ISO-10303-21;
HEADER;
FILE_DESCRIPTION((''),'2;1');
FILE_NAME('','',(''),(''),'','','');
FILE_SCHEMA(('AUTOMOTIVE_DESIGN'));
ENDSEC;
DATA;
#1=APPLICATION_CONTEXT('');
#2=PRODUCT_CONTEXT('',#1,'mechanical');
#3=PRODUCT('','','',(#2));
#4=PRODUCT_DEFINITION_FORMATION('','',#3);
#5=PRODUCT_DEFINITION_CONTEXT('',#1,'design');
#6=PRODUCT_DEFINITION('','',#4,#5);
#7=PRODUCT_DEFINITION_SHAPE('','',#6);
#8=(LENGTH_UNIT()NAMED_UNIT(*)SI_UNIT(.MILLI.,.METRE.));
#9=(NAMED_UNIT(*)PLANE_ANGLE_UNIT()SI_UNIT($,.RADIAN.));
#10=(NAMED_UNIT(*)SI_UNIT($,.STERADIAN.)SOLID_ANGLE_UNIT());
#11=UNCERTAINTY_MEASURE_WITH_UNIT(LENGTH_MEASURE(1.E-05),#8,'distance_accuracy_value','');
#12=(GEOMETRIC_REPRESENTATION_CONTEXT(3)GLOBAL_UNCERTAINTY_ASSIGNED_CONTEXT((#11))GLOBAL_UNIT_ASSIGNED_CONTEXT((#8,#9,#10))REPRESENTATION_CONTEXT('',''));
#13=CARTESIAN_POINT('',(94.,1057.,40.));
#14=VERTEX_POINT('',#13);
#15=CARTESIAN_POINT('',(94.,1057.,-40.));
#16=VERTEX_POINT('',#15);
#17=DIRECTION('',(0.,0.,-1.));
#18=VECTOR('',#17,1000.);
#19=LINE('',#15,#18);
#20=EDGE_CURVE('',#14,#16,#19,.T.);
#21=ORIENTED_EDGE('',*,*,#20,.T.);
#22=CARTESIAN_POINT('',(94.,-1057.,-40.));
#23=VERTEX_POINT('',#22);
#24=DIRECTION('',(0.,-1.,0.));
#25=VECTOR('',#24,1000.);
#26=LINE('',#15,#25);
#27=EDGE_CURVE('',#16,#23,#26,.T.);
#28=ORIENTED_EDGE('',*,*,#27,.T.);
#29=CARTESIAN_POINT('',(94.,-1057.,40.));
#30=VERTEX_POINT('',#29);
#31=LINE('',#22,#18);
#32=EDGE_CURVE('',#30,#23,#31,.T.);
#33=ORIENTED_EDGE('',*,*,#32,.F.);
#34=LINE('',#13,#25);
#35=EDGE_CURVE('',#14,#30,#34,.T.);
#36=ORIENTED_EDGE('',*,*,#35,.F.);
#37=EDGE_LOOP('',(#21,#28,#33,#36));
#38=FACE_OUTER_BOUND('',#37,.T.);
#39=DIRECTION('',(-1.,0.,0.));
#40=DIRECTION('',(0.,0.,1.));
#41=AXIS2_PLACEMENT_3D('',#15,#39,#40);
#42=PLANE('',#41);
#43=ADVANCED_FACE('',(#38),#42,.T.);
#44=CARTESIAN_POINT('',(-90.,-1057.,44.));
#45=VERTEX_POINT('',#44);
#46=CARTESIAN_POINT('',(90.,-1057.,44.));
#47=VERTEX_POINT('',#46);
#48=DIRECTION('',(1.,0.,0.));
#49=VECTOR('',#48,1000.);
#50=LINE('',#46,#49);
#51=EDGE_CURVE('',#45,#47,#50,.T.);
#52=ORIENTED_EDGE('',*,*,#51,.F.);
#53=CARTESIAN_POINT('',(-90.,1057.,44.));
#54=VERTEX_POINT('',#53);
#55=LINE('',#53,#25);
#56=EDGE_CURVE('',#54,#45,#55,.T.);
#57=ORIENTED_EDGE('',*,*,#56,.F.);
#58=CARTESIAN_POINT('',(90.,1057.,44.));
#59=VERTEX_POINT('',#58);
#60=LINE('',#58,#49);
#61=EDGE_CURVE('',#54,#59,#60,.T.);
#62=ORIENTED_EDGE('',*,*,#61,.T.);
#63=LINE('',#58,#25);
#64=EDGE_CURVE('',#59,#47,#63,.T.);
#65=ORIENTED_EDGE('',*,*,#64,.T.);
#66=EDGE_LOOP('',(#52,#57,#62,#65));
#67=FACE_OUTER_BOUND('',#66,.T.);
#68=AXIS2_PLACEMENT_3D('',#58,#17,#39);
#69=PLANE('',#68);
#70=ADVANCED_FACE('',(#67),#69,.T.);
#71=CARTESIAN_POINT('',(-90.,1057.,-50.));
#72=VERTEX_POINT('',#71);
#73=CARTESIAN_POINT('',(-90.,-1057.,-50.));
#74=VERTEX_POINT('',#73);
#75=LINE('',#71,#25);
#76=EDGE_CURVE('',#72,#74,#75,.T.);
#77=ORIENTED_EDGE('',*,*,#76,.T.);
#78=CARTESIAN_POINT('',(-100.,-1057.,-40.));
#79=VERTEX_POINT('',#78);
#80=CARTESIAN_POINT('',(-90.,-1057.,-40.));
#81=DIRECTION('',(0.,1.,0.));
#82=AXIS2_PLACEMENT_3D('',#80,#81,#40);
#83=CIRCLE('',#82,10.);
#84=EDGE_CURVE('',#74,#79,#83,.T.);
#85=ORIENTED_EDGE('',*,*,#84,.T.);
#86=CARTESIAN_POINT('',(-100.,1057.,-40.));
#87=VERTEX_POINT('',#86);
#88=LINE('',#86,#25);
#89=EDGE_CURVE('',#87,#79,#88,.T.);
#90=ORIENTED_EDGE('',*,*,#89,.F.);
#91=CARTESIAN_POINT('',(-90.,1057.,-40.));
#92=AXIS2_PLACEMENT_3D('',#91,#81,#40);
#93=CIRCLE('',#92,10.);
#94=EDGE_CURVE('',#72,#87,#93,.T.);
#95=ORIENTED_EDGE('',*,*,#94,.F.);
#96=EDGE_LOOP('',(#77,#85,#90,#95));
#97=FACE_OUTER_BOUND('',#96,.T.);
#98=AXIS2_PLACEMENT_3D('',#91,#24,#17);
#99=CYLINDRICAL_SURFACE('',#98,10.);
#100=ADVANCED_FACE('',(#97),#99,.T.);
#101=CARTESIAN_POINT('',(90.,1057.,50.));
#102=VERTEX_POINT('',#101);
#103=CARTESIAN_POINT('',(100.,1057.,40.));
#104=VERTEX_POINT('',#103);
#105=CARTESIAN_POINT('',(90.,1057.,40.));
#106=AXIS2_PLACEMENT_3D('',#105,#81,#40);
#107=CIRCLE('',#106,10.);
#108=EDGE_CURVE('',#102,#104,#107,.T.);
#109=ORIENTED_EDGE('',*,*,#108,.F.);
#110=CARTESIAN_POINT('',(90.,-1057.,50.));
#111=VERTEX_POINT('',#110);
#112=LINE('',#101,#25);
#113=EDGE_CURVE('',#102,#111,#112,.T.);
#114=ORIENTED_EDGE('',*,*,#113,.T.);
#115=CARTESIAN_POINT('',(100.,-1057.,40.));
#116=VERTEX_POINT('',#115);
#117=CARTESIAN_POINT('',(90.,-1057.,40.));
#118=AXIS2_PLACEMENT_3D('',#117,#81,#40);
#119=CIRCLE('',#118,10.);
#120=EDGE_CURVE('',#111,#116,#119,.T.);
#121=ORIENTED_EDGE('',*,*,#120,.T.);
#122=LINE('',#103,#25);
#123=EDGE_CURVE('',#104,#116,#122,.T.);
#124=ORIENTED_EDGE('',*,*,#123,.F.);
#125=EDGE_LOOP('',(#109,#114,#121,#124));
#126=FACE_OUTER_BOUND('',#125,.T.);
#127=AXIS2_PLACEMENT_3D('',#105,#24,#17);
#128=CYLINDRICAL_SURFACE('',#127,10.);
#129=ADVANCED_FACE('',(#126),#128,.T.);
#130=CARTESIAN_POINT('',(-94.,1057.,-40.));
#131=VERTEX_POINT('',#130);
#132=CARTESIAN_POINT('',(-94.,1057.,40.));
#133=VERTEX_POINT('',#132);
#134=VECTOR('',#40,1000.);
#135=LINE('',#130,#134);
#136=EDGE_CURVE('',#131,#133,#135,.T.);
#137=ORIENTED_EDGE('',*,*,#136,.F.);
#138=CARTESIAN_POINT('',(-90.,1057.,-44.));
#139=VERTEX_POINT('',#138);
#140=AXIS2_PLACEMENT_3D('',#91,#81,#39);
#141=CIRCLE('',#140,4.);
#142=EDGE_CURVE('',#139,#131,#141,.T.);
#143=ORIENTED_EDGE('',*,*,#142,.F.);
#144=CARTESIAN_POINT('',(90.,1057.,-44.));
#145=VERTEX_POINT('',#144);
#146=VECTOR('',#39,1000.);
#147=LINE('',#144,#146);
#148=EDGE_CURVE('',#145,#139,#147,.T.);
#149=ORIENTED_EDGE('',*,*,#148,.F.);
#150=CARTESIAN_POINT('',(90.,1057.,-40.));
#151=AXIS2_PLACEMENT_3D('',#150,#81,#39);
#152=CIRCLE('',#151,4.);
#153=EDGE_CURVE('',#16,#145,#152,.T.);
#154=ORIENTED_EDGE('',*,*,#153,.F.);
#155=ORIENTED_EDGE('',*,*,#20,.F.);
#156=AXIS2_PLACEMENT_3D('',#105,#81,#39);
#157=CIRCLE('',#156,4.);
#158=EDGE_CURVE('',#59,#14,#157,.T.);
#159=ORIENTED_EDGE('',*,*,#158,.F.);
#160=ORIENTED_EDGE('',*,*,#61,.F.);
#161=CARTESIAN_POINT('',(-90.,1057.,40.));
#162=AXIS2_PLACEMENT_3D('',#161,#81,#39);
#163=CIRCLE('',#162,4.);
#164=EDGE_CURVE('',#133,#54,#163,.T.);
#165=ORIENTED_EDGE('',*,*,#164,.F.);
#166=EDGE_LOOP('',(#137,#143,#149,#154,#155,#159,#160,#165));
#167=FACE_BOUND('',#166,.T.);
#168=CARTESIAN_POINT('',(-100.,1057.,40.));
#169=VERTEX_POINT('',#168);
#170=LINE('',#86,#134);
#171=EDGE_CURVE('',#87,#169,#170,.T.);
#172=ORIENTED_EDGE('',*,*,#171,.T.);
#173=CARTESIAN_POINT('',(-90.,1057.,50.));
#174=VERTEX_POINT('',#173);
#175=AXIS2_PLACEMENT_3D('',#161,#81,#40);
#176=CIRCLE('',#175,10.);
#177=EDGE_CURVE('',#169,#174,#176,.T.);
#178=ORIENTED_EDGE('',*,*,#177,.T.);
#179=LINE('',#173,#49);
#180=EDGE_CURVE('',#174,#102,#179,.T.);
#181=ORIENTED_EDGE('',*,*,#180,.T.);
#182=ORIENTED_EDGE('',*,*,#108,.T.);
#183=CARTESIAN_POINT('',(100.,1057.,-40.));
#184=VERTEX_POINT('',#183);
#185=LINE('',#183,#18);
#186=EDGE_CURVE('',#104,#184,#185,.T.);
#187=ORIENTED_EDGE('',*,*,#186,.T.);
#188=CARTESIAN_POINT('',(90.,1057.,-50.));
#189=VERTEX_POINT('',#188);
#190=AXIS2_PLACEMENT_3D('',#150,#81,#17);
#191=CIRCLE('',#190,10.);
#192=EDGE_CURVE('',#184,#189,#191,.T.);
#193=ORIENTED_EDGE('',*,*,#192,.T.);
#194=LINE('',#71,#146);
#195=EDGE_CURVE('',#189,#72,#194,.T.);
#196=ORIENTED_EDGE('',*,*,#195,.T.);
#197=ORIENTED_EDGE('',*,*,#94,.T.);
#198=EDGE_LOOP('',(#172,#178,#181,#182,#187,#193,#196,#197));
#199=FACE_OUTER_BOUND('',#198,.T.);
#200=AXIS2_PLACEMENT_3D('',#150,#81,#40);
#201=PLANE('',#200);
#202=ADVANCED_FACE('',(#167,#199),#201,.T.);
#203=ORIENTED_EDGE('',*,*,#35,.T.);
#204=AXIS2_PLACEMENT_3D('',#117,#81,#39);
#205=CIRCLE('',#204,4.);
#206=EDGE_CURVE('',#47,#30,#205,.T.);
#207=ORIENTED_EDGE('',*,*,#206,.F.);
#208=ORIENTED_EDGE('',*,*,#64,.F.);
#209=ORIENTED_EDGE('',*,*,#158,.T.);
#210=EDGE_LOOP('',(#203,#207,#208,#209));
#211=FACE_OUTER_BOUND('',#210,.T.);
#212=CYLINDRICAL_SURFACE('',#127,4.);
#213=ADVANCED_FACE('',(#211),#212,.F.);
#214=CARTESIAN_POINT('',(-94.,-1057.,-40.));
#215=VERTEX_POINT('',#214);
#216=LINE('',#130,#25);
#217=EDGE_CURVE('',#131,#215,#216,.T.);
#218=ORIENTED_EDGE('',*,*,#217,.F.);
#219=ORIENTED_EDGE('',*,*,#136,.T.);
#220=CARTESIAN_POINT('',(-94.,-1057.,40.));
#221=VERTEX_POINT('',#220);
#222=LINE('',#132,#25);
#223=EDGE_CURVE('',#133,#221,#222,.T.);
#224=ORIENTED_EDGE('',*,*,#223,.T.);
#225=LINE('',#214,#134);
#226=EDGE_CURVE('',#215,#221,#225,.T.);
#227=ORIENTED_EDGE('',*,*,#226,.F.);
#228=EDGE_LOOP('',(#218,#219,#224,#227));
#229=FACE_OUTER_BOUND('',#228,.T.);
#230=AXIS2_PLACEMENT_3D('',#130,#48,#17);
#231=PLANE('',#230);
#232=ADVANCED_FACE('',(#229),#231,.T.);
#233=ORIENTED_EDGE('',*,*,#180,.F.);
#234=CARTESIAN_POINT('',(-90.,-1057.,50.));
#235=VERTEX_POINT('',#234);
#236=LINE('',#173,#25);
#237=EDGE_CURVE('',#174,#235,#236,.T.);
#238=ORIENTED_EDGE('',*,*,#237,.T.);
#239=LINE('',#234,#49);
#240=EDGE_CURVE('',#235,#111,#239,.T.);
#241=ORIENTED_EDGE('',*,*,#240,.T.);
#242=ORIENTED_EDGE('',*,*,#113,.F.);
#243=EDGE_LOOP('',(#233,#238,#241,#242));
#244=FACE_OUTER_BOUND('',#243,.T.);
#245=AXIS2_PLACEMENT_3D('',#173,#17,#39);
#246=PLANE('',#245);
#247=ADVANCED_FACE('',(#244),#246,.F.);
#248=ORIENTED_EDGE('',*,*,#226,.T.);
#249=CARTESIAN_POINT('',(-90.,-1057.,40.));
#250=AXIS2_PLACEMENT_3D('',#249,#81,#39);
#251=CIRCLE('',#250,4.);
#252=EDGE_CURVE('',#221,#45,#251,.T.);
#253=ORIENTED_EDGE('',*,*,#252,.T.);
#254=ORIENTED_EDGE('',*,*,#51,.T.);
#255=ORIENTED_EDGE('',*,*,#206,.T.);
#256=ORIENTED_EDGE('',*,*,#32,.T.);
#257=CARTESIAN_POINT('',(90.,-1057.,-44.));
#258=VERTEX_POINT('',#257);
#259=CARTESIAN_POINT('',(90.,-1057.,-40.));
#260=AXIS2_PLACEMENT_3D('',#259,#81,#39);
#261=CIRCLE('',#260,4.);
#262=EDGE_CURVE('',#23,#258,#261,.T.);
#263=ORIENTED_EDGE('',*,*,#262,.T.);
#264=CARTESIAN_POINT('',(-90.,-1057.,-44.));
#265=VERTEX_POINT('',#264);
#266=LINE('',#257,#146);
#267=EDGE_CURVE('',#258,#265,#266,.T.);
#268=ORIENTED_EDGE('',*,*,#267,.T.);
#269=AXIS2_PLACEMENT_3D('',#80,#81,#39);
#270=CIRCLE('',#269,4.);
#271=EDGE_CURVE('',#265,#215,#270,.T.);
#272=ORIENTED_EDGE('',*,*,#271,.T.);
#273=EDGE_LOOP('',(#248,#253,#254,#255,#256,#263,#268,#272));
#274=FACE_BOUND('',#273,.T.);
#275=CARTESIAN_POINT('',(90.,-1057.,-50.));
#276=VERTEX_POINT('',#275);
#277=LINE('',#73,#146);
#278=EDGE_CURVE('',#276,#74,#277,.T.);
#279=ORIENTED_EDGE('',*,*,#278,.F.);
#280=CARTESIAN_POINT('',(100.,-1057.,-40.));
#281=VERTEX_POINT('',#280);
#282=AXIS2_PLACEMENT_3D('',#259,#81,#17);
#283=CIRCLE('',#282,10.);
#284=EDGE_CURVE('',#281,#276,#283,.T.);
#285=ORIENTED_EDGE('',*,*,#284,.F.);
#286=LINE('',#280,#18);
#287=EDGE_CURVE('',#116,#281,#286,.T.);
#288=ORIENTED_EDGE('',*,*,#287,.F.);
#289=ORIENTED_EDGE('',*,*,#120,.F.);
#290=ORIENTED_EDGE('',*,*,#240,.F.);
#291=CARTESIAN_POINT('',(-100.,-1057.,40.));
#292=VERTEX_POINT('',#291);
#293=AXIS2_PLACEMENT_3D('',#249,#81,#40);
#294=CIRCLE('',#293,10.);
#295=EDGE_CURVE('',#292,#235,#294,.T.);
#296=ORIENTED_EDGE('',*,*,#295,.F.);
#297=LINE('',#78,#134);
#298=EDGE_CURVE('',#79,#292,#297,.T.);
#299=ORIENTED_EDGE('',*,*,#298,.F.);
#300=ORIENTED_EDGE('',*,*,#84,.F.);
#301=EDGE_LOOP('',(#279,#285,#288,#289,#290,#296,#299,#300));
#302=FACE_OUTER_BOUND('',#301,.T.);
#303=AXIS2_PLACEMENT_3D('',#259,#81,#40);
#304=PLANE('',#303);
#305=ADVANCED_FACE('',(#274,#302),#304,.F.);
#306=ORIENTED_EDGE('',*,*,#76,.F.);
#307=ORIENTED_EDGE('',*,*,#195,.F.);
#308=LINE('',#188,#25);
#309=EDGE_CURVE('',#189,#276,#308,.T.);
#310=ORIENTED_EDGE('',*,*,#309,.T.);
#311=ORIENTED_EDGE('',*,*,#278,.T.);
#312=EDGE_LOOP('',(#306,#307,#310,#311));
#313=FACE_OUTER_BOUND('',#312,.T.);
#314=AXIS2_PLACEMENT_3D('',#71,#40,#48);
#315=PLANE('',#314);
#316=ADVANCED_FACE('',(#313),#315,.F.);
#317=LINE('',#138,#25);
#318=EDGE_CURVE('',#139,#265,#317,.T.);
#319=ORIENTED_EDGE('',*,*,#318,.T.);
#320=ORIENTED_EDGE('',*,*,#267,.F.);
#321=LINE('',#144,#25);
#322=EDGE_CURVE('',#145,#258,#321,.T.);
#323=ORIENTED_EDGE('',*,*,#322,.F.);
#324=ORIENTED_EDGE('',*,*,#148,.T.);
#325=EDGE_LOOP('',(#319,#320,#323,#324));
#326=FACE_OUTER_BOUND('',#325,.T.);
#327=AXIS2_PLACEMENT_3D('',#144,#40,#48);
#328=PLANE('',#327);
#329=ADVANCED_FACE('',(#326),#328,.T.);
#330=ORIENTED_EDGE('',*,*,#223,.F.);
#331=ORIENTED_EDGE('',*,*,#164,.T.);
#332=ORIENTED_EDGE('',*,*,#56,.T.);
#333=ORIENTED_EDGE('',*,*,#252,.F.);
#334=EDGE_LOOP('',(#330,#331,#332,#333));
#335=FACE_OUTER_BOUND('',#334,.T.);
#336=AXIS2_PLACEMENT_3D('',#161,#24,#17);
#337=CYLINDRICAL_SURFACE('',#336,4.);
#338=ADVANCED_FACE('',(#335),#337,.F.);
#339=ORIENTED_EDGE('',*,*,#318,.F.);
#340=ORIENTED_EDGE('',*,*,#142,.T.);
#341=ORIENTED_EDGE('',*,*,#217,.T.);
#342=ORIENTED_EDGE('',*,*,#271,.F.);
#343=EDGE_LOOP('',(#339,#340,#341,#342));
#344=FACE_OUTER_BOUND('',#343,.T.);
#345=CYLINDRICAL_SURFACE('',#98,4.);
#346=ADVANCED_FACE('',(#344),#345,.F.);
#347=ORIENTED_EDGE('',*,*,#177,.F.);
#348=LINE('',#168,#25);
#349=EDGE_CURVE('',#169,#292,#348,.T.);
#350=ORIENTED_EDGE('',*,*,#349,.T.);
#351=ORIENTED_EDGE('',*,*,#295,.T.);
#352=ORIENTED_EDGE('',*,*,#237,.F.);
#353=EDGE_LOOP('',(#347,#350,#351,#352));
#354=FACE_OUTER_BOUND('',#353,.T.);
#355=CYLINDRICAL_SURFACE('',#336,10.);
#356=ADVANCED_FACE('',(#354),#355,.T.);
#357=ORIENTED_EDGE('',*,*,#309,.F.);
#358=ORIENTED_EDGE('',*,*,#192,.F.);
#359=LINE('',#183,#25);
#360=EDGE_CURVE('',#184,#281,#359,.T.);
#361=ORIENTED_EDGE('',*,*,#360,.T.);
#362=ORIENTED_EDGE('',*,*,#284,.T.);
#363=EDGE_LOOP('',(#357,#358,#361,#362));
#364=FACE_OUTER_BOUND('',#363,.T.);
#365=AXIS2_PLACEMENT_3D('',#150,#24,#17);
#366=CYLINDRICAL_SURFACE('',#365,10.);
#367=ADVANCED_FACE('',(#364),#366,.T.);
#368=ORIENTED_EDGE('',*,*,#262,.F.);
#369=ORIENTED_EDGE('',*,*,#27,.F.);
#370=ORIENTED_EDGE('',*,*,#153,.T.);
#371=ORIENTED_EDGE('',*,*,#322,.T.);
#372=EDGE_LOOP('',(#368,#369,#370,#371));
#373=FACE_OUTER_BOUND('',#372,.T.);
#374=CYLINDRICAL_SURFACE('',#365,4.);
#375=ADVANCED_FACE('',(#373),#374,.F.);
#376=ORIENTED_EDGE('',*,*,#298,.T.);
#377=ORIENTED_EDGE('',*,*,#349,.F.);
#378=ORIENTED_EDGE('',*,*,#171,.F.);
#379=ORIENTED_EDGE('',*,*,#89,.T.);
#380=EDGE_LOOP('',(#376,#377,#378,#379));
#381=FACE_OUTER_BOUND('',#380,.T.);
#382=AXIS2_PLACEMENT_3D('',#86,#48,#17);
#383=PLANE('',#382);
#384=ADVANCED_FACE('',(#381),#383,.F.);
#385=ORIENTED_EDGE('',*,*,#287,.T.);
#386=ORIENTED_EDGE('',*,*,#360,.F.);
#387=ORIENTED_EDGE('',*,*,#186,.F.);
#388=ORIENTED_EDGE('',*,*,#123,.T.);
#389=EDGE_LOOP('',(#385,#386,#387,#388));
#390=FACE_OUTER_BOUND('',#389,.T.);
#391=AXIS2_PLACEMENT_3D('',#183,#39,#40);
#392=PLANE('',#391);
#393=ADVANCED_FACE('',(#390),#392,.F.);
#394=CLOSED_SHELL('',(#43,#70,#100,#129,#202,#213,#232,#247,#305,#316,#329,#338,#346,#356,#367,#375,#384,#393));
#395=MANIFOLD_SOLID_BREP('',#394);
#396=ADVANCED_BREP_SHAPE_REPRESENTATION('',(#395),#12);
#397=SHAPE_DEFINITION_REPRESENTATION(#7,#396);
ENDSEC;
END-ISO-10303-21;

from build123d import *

# Parameters (mm, degrees)
EXTRUDE_THIN1_DEPTH = 1057


with BuildPart() as part:
    # Sketch1 → Extrude-Thin1 (new, symmetric)
    with BuildSketch(Plane(origin=(0, 0, 0), x_dir=(1, 0, 0), z_dir=(0, 1, 0))):
        with BuildLine():
            Line((-90, 50), (90, 50))
            ThreePointArc((90, 50), (97.071067812, 47.071067812), (100, 40))
            Line((100, 40), (100, -40))
            ThreePointArc((100, -40), (97.071067812, -47.071067812), (90, -50))
            Line((90, -50), (-90, -50))
            ThreePointArc((-90, -50), (-97.071067812, -47.071067812), (-100, -40))
            Line((-100, -40), (-100, 40))
            ThreePointArc((-100, 40), (-97.071067812, 47.071067812), (-90, 50))
        make_face()
        with BuildLine():
            Line((-90, 44), (90, 44))
            ThreePointArc((90, 44), (92.828427125, 42.828427125), (94, 40))
            Line((94, 40), (94, -40))
            ThreePointArc((94, -40), (92.828427125, -42.828427125), (90, -44))
            Line((90, -44), (-90, -44))
            ThreePointArc((-90, -44), (-92.828427125, -42.828427125), (-94, -40))
            Line((-94, -40), (-94, 40))
            ThreePointArc((-94, 40), (-92.828427125, 42.828427125), (-90, 44))
        make_face(mode=Mode.SUBTRACT)
    extrude(amount=EXTRUDE_THIN1_DEPTH, both=True)


solid = part.part
